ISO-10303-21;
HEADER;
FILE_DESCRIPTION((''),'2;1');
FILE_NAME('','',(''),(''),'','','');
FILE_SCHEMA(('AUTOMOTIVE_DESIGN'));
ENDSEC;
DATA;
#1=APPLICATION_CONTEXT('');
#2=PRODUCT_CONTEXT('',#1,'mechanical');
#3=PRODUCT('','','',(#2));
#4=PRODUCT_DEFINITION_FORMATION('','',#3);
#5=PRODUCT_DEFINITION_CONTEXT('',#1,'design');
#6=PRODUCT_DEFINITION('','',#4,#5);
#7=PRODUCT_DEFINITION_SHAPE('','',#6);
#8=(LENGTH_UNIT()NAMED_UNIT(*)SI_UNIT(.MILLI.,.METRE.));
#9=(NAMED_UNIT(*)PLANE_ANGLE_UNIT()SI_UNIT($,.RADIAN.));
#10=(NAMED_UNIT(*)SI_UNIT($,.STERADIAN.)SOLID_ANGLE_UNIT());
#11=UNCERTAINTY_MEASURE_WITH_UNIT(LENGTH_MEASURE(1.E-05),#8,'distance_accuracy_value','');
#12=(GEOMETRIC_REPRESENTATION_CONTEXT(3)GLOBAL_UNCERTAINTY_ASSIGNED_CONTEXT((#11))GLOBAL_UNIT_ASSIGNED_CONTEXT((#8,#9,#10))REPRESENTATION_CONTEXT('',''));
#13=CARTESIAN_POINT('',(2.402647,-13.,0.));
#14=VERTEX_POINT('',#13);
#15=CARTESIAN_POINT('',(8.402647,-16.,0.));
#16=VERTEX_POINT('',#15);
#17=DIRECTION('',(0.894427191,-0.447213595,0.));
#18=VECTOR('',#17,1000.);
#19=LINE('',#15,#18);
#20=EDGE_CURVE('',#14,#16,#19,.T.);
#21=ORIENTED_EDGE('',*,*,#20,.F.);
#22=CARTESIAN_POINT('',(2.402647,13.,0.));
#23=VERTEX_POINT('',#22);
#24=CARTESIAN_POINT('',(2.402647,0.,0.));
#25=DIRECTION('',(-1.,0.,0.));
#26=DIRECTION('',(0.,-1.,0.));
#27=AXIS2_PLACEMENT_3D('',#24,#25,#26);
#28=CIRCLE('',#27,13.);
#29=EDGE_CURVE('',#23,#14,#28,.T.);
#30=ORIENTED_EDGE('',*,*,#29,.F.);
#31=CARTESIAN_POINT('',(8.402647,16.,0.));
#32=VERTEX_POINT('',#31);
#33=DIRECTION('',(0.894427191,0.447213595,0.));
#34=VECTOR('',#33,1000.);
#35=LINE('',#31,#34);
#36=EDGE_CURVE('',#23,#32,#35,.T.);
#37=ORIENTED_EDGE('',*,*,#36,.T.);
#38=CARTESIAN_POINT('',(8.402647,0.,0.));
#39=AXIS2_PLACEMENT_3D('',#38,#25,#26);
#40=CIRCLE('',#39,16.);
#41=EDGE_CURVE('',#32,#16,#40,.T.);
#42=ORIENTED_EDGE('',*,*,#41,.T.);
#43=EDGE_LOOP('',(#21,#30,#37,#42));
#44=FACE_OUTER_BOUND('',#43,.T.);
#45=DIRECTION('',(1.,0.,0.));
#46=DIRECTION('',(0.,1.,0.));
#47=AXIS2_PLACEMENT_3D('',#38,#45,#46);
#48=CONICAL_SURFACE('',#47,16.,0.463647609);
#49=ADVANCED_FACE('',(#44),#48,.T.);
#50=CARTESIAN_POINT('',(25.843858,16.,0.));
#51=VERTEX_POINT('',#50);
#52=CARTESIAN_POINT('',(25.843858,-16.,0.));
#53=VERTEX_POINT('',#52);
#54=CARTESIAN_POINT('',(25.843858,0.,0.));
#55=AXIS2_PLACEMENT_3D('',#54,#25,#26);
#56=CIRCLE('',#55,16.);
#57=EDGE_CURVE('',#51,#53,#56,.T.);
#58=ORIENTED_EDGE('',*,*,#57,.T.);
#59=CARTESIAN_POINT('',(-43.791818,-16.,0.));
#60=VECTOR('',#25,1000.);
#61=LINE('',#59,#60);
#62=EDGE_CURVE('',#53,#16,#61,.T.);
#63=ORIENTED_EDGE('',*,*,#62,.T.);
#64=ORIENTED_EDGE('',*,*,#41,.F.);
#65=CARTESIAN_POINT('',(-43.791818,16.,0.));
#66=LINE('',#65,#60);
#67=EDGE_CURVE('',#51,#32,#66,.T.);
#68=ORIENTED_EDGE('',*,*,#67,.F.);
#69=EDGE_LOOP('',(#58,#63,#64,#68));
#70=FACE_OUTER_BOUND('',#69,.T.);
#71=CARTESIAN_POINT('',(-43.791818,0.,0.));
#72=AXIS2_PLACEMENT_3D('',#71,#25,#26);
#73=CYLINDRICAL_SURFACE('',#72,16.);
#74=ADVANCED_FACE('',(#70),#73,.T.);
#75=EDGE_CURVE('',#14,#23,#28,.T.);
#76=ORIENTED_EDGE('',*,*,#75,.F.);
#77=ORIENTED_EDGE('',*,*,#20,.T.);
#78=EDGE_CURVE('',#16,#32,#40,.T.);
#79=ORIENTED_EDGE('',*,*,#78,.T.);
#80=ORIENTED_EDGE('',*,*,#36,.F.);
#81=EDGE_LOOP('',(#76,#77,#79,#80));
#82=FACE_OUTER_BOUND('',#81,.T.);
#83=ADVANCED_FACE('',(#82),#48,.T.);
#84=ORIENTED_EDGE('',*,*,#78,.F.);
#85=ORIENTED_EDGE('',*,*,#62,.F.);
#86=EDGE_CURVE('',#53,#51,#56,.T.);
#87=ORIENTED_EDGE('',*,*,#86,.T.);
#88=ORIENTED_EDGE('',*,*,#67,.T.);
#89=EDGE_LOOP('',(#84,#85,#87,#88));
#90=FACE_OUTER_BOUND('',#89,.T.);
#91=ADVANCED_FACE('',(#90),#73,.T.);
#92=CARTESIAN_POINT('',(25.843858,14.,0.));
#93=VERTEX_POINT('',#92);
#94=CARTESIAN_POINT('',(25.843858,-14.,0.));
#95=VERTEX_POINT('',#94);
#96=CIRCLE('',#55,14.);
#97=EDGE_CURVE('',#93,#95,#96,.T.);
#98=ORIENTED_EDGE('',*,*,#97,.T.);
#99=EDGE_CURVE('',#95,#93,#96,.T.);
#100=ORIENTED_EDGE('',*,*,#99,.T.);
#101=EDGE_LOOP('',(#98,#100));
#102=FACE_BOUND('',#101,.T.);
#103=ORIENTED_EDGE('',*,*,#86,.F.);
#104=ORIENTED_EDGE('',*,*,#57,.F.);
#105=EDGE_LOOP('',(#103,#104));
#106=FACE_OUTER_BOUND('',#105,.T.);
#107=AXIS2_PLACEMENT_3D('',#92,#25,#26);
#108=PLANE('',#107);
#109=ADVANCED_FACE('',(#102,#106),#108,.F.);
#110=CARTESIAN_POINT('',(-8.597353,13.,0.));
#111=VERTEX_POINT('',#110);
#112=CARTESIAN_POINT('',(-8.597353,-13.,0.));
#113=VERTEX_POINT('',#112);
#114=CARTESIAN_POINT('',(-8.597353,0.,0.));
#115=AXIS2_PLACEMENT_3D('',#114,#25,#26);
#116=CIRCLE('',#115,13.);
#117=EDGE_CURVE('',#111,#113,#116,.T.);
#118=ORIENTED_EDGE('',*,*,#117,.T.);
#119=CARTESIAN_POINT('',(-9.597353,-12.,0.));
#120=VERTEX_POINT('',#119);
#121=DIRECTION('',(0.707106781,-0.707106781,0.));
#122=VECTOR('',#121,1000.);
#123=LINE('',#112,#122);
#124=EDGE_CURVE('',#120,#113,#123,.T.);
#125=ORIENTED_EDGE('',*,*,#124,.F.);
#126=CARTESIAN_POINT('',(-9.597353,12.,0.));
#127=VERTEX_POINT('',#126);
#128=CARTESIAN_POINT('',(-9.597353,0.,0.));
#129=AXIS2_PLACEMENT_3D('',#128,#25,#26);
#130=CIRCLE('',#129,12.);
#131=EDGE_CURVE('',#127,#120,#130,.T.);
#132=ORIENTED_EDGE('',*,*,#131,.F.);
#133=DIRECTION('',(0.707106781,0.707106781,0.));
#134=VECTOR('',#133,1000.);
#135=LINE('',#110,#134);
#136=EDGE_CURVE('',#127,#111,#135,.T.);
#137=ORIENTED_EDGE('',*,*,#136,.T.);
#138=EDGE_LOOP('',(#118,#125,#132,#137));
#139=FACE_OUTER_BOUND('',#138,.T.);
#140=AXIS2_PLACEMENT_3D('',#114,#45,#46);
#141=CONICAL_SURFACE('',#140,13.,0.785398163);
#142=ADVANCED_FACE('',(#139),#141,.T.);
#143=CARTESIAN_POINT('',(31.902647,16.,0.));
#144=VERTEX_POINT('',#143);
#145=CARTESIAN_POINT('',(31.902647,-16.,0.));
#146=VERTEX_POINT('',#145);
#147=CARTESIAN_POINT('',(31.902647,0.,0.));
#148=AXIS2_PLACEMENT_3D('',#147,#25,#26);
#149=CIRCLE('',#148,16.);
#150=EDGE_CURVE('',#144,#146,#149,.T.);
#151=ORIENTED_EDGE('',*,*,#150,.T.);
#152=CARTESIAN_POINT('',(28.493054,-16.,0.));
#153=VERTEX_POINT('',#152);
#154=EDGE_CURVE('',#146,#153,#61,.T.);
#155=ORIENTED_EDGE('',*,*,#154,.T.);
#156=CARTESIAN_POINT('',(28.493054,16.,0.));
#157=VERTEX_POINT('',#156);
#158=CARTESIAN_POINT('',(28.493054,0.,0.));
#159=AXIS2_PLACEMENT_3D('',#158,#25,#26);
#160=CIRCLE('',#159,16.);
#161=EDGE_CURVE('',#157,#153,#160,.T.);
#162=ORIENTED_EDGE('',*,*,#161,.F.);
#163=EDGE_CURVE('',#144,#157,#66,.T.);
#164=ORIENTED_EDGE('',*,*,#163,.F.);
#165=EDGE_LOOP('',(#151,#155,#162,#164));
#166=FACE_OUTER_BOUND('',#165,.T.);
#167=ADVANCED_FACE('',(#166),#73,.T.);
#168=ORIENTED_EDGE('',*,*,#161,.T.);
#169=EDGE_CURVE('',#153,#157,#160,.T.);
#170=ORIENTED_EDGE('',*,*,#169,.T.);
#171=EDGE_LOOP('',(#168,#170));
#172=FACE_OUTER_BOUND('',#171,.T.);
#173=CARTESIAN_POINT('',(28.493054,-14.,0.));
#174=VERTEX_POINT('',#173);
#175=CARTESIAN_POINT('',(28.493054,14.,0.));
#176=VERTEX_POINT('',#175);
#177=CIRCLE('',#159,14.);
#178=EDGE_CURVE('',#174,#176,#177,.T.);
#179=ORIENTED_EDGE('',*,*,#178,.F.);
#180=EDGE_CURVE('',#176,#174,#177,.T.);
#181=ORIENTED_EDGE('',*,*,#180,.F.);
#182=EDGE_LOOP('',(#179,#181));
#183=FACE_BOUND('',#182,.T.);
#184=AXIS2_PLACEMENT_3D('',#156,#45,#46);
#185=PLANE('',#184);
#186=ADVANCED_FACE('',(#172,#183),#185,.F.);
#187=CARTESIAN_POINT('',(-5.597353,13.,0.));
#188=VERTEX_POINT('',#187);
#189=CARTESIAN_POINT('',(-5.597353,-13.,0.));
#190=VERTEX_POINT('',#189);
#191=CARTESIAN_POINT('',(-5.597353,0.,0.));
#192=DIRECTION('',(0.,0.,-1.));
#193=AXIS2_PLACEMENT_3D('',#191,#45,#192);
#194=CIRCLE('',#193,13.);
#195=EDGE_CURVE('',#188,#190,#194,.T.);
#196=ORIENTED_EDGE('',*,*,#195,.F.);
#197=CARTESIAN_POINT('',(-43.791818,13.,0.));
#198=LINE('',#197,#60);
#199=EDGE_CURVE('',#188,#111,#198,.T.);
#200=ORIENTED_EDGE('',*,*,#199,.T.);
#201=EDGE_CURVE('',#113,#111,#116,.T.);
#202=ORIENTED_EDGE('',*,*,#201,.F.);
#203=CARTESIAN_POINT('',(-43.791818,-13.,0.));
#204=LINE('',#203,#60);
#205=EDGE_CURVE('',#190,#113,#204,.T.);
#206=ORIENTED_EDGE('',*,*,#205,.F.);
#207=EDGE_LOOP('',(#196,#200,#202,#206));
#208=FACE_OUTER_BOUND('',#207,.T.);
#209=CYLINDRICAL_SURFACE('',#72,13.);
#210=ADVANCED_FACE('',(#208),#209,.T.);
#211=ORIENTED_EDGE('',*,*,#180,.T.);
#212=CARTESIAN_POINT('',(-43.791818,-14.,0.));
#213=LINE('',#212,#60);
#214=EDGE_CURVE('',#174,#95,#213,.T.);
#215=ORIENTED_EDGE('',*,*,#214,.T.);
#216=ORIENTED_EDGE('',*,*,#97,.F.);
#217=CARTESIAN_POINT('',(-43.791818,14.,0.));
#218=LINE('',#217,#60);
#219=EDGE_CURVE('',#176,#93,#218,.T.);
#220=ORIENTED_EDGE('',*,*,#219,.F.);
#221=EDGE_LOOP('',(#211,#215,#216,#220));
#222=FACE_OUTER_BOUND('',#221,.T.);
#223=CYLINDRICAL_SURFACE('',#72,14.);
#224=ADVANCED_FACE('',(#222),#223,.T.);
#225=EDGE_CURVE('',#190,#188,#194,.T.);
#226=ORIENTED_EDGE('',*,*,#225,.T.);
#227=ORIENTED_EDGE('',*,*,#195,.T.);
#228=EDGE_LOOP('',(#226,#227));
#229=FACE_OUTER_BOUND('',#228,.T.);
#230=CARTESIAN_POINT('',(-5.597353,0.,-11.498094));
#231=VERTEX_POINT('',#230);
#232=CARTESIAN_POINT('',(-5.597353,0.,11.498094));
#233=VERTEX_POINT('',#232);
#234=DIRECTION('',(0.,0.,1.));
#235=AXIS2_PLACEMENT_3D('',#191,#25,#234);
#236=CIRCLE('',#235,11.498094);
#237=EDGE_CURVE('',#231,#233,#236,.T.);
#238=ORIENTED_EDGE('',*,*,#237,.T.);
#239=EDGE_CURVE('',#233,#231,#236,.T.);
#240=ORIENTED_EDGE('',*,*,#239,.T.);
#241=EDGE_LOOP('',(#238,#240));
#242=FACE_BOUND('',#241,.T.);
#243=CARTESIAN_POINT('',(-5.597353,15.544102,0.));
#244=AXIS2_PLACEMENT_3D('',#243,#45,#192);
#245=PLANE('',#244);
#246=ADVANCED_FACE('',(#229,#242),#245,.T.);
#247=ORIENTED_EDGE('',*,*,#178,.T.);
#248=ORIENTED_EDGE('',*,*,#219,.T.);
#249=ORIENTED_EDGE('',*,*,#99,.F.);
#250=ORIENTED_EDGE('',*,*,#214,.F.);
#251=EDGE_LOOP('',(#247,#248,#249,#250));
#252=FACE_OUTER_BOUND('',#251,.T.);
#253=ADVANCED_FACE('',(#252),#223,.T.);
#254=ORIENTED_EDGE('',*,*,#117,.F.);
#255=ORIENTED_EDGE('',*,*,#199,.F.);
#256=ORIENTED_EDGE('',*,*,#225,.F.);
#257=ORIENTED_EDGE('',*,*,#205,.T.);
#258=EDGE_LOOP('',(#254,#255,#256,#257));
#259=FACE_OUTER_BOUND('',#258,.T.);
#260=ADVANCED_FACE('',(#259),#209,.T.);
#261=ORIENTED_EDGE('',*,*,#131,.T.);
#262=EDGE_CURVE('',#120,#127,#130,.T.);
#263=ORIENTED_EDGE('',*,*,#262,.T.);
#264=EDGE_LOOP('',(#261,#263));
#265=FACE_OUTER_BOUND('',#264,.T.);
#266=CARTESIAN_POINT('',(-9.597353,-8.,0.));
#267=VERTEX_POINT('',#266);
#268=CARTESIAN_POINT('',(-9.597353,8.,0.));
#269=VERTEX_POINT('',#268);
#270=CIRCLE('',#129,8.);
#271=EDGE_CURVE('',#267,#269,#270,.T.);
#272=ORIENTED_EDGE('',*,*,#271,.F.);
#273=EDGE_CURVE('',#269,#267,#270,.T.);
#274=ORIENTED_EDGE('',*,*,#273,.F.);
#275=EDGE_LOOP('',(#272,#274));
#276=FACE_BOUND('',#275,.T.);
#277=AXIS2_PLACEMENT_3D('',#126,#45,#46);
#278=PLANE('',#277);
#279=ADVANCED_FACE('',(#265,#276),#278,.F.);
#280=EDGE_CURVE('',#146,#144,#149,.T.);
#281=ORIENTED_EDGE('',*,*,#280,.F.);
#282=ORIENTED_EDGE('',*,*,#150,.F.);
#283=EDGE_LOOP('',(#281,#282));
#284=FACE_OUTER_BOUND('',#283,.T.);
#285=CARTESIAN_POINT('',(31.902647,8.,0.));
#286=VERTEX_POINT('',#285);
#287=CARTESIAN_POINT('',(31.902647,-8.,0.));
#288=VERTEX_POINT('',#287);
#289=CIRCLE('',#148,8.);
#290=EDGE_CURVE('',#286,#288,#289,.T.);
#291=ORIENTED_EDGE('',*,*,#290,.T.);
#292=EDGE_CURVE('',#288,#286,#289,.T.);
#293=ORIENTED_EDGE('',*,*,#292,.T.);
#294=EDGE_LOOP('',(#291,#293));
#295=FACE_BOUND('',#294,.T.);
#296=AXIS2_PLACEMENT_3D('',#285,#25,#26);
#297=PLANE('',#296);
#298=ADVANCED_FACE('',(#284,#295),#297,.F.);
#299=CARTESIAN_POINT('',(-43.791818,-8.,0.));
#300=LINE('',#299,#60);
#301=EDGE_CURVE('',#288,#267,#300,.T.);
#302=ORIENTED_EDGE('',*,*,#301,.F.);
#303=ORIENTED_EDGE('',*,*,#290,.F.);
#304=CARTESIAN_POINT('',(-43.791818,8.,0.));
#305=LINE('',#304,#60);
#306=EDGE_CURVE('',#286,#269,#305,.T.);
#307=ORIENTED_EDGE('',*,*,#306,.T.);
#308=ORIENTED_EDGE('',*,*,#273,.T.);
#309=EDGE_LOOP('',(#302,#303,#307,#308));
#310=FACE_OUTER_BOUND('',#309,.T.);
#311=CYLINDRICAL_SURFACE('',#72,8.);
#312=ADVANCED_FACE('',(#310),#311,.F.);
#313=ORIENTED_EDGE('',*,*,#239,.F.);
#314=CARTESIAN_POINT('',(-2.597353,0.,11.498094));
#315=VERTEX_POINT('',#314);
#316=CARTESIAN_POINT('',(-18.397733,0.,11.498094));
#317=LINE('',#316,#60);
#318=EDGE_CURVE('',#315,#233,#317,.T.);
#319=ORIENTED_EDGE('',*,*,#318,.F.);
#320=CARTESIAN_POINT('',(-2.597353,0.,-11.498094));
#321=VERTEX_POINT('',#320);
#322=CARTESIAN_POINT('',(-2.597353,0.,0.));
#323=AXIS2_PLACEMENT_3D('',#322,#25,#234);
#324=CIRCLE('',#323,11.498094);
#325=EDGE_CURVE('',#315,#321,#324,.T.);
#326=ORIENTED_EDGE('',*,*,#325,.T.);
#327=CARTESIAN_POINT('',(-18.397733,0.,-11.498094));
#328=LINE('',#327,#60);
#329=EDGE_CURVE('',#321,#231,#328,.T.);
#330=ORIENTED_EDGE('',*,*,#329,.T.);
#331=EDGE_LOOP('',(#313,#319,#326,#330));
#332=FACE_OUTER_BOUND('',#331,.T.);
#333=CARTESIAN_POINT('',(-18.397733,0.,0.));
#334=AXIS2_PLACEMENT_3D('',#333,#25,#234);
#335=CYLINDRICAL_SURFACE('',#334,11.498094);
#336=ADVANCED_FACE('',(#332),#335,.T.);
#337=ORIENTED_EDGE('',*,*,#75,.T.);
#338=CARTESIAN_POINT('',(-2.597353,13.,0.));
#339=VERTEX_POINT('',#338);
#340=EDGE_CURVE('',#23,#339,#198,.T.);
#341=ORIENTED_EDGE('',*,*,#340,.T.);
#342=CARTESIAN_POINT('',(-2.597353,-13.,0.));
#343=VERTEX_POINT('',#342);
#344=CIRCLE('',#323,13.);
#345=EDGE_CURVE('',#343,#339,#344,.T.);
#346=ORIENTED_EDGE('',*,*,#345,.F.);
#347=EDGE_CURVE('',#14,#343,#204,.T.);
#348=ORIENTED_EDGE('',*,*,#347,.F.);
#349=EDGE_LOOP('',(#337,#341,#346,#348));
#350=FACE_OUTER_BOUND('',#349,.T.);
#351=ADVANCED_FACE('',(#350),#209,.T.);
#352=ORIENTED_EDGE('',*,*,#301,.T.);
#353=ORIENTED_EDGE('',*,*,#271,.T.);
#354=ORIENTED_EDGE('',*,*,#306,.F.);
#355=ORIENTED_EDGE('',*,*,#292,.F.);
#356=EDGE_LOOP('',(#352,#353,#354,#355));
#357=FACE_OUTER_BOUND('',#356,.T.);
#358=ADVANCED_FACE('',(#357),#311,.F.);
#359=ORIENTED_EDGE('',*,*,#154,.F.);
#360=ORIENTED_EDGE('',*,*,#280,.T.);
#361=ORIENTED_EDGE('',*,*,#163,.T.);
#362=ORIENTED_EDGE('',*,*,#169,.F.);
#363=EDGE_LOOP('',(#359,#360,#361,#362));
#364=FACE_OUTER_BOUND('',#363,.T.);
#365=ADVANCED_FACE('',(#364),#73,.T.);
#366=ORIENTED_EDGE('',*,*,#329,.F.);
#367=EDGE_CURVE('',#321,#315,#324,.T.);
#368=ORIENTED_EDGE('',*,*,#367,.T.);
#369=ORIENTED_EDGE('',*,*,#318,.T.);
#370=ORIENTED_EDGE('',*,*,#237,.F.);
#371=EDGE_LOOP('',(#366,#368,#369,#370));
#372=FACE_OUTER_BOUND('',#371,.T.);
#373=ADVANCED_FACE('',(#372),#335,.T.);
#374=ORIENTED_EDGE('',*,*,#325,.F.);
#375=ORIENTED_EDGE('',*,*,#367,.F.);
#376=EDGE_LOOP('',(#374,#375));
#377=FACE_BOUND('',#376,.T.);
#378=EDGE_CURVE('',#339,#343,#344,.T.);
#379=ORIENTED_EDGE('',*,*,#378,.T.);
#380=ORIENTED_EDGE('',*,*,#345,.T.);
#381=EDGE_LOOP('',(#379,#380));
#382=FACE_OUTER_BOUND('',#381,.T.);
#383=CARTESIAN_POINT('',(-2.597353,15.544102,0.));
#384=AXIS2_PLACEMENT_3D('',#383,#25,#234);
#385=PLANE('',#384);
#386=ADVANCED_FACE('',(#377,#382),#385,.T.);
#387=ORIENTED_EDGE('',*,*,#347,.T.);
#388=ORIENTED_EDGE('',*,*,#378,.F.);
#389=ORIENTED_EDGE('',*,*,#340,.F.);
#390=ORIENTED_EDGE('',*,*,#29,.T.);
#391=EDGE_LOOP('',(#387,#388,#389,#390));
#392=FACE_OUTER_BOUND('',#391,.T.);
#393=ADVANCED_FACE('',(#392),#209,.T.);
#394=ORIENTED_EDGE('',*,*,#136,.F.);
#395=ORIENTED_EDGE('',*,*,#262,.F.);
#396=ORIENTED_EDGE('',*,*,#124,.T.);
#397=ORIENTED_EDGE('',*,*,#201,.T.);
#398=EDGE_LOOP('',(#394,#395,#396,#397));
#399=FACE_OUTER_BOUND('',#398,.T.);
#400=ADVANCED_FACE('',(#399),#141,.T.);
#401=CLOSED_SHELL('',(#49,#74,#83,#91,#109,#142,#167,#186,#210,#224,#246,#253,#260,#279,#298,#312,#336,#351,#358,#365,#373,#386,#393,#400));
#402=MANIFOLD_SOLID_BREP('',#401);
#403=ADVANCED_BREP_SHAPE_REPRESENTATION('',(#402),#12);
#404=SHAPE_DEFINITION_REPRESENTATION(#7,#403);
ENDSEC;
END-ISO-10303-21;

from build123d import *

# Parameters (mm, degrees)
GROOVE_PROFILE_SKETCH_3X3_W = 3
GROOVE_PROFILE_SKETCH_3X3_H = 4.04600801


with BuildPart() as part:
    # Bushing Profile Sketch → Bushing Body Revolve (revolve)
    with BuildSketch(Plane.XY, mode=Mode.PRIVATE) as bushing_body_revolve_sk:
        Polygon((-9.597352736, 8), (31.902647264, 8), (31.902647264, 16), (28.493054394, 16), (28.493054394, 14), (25.843857713, 14), (25.843857713, 16), (8.402647264, 16), (2.402647264, 13), (-8.597352736, 13), (-9.597352736, 12), align=None)
    revolve(bushing_body_revolve_sk.sketch.rotate(Axis((-43.791817978, 0, 0), (1, 0, 0)), 180), axis=Axis((-43.791817978, 0, 0), (1, 0, 0)))

    # Groove Profile Sketch 3x3 → Groove Cut 3x3 (revolve, cut)
    with BuildSketch(Plane.XY, mode=Mode.PRIVATE) as groove_cut_3x3_sk:
        with Locations((-4.097352736, 13.5210982)):
            Rectangle(GROOVE_PROFILE_SKETCH_3X3_W, GROOVE_PROFILE_SKETCH_3X3_H)
    revolve(groove_cut_3x3_sk.sketch.rotate(Axis((-18.397733025, 0, 0), (1, 0, 0)), 180), axis=Axis((-18.397733025, 0, 0), (1, 0, 0)), mode=Mode.SUBTRACT)


solid = part.part
